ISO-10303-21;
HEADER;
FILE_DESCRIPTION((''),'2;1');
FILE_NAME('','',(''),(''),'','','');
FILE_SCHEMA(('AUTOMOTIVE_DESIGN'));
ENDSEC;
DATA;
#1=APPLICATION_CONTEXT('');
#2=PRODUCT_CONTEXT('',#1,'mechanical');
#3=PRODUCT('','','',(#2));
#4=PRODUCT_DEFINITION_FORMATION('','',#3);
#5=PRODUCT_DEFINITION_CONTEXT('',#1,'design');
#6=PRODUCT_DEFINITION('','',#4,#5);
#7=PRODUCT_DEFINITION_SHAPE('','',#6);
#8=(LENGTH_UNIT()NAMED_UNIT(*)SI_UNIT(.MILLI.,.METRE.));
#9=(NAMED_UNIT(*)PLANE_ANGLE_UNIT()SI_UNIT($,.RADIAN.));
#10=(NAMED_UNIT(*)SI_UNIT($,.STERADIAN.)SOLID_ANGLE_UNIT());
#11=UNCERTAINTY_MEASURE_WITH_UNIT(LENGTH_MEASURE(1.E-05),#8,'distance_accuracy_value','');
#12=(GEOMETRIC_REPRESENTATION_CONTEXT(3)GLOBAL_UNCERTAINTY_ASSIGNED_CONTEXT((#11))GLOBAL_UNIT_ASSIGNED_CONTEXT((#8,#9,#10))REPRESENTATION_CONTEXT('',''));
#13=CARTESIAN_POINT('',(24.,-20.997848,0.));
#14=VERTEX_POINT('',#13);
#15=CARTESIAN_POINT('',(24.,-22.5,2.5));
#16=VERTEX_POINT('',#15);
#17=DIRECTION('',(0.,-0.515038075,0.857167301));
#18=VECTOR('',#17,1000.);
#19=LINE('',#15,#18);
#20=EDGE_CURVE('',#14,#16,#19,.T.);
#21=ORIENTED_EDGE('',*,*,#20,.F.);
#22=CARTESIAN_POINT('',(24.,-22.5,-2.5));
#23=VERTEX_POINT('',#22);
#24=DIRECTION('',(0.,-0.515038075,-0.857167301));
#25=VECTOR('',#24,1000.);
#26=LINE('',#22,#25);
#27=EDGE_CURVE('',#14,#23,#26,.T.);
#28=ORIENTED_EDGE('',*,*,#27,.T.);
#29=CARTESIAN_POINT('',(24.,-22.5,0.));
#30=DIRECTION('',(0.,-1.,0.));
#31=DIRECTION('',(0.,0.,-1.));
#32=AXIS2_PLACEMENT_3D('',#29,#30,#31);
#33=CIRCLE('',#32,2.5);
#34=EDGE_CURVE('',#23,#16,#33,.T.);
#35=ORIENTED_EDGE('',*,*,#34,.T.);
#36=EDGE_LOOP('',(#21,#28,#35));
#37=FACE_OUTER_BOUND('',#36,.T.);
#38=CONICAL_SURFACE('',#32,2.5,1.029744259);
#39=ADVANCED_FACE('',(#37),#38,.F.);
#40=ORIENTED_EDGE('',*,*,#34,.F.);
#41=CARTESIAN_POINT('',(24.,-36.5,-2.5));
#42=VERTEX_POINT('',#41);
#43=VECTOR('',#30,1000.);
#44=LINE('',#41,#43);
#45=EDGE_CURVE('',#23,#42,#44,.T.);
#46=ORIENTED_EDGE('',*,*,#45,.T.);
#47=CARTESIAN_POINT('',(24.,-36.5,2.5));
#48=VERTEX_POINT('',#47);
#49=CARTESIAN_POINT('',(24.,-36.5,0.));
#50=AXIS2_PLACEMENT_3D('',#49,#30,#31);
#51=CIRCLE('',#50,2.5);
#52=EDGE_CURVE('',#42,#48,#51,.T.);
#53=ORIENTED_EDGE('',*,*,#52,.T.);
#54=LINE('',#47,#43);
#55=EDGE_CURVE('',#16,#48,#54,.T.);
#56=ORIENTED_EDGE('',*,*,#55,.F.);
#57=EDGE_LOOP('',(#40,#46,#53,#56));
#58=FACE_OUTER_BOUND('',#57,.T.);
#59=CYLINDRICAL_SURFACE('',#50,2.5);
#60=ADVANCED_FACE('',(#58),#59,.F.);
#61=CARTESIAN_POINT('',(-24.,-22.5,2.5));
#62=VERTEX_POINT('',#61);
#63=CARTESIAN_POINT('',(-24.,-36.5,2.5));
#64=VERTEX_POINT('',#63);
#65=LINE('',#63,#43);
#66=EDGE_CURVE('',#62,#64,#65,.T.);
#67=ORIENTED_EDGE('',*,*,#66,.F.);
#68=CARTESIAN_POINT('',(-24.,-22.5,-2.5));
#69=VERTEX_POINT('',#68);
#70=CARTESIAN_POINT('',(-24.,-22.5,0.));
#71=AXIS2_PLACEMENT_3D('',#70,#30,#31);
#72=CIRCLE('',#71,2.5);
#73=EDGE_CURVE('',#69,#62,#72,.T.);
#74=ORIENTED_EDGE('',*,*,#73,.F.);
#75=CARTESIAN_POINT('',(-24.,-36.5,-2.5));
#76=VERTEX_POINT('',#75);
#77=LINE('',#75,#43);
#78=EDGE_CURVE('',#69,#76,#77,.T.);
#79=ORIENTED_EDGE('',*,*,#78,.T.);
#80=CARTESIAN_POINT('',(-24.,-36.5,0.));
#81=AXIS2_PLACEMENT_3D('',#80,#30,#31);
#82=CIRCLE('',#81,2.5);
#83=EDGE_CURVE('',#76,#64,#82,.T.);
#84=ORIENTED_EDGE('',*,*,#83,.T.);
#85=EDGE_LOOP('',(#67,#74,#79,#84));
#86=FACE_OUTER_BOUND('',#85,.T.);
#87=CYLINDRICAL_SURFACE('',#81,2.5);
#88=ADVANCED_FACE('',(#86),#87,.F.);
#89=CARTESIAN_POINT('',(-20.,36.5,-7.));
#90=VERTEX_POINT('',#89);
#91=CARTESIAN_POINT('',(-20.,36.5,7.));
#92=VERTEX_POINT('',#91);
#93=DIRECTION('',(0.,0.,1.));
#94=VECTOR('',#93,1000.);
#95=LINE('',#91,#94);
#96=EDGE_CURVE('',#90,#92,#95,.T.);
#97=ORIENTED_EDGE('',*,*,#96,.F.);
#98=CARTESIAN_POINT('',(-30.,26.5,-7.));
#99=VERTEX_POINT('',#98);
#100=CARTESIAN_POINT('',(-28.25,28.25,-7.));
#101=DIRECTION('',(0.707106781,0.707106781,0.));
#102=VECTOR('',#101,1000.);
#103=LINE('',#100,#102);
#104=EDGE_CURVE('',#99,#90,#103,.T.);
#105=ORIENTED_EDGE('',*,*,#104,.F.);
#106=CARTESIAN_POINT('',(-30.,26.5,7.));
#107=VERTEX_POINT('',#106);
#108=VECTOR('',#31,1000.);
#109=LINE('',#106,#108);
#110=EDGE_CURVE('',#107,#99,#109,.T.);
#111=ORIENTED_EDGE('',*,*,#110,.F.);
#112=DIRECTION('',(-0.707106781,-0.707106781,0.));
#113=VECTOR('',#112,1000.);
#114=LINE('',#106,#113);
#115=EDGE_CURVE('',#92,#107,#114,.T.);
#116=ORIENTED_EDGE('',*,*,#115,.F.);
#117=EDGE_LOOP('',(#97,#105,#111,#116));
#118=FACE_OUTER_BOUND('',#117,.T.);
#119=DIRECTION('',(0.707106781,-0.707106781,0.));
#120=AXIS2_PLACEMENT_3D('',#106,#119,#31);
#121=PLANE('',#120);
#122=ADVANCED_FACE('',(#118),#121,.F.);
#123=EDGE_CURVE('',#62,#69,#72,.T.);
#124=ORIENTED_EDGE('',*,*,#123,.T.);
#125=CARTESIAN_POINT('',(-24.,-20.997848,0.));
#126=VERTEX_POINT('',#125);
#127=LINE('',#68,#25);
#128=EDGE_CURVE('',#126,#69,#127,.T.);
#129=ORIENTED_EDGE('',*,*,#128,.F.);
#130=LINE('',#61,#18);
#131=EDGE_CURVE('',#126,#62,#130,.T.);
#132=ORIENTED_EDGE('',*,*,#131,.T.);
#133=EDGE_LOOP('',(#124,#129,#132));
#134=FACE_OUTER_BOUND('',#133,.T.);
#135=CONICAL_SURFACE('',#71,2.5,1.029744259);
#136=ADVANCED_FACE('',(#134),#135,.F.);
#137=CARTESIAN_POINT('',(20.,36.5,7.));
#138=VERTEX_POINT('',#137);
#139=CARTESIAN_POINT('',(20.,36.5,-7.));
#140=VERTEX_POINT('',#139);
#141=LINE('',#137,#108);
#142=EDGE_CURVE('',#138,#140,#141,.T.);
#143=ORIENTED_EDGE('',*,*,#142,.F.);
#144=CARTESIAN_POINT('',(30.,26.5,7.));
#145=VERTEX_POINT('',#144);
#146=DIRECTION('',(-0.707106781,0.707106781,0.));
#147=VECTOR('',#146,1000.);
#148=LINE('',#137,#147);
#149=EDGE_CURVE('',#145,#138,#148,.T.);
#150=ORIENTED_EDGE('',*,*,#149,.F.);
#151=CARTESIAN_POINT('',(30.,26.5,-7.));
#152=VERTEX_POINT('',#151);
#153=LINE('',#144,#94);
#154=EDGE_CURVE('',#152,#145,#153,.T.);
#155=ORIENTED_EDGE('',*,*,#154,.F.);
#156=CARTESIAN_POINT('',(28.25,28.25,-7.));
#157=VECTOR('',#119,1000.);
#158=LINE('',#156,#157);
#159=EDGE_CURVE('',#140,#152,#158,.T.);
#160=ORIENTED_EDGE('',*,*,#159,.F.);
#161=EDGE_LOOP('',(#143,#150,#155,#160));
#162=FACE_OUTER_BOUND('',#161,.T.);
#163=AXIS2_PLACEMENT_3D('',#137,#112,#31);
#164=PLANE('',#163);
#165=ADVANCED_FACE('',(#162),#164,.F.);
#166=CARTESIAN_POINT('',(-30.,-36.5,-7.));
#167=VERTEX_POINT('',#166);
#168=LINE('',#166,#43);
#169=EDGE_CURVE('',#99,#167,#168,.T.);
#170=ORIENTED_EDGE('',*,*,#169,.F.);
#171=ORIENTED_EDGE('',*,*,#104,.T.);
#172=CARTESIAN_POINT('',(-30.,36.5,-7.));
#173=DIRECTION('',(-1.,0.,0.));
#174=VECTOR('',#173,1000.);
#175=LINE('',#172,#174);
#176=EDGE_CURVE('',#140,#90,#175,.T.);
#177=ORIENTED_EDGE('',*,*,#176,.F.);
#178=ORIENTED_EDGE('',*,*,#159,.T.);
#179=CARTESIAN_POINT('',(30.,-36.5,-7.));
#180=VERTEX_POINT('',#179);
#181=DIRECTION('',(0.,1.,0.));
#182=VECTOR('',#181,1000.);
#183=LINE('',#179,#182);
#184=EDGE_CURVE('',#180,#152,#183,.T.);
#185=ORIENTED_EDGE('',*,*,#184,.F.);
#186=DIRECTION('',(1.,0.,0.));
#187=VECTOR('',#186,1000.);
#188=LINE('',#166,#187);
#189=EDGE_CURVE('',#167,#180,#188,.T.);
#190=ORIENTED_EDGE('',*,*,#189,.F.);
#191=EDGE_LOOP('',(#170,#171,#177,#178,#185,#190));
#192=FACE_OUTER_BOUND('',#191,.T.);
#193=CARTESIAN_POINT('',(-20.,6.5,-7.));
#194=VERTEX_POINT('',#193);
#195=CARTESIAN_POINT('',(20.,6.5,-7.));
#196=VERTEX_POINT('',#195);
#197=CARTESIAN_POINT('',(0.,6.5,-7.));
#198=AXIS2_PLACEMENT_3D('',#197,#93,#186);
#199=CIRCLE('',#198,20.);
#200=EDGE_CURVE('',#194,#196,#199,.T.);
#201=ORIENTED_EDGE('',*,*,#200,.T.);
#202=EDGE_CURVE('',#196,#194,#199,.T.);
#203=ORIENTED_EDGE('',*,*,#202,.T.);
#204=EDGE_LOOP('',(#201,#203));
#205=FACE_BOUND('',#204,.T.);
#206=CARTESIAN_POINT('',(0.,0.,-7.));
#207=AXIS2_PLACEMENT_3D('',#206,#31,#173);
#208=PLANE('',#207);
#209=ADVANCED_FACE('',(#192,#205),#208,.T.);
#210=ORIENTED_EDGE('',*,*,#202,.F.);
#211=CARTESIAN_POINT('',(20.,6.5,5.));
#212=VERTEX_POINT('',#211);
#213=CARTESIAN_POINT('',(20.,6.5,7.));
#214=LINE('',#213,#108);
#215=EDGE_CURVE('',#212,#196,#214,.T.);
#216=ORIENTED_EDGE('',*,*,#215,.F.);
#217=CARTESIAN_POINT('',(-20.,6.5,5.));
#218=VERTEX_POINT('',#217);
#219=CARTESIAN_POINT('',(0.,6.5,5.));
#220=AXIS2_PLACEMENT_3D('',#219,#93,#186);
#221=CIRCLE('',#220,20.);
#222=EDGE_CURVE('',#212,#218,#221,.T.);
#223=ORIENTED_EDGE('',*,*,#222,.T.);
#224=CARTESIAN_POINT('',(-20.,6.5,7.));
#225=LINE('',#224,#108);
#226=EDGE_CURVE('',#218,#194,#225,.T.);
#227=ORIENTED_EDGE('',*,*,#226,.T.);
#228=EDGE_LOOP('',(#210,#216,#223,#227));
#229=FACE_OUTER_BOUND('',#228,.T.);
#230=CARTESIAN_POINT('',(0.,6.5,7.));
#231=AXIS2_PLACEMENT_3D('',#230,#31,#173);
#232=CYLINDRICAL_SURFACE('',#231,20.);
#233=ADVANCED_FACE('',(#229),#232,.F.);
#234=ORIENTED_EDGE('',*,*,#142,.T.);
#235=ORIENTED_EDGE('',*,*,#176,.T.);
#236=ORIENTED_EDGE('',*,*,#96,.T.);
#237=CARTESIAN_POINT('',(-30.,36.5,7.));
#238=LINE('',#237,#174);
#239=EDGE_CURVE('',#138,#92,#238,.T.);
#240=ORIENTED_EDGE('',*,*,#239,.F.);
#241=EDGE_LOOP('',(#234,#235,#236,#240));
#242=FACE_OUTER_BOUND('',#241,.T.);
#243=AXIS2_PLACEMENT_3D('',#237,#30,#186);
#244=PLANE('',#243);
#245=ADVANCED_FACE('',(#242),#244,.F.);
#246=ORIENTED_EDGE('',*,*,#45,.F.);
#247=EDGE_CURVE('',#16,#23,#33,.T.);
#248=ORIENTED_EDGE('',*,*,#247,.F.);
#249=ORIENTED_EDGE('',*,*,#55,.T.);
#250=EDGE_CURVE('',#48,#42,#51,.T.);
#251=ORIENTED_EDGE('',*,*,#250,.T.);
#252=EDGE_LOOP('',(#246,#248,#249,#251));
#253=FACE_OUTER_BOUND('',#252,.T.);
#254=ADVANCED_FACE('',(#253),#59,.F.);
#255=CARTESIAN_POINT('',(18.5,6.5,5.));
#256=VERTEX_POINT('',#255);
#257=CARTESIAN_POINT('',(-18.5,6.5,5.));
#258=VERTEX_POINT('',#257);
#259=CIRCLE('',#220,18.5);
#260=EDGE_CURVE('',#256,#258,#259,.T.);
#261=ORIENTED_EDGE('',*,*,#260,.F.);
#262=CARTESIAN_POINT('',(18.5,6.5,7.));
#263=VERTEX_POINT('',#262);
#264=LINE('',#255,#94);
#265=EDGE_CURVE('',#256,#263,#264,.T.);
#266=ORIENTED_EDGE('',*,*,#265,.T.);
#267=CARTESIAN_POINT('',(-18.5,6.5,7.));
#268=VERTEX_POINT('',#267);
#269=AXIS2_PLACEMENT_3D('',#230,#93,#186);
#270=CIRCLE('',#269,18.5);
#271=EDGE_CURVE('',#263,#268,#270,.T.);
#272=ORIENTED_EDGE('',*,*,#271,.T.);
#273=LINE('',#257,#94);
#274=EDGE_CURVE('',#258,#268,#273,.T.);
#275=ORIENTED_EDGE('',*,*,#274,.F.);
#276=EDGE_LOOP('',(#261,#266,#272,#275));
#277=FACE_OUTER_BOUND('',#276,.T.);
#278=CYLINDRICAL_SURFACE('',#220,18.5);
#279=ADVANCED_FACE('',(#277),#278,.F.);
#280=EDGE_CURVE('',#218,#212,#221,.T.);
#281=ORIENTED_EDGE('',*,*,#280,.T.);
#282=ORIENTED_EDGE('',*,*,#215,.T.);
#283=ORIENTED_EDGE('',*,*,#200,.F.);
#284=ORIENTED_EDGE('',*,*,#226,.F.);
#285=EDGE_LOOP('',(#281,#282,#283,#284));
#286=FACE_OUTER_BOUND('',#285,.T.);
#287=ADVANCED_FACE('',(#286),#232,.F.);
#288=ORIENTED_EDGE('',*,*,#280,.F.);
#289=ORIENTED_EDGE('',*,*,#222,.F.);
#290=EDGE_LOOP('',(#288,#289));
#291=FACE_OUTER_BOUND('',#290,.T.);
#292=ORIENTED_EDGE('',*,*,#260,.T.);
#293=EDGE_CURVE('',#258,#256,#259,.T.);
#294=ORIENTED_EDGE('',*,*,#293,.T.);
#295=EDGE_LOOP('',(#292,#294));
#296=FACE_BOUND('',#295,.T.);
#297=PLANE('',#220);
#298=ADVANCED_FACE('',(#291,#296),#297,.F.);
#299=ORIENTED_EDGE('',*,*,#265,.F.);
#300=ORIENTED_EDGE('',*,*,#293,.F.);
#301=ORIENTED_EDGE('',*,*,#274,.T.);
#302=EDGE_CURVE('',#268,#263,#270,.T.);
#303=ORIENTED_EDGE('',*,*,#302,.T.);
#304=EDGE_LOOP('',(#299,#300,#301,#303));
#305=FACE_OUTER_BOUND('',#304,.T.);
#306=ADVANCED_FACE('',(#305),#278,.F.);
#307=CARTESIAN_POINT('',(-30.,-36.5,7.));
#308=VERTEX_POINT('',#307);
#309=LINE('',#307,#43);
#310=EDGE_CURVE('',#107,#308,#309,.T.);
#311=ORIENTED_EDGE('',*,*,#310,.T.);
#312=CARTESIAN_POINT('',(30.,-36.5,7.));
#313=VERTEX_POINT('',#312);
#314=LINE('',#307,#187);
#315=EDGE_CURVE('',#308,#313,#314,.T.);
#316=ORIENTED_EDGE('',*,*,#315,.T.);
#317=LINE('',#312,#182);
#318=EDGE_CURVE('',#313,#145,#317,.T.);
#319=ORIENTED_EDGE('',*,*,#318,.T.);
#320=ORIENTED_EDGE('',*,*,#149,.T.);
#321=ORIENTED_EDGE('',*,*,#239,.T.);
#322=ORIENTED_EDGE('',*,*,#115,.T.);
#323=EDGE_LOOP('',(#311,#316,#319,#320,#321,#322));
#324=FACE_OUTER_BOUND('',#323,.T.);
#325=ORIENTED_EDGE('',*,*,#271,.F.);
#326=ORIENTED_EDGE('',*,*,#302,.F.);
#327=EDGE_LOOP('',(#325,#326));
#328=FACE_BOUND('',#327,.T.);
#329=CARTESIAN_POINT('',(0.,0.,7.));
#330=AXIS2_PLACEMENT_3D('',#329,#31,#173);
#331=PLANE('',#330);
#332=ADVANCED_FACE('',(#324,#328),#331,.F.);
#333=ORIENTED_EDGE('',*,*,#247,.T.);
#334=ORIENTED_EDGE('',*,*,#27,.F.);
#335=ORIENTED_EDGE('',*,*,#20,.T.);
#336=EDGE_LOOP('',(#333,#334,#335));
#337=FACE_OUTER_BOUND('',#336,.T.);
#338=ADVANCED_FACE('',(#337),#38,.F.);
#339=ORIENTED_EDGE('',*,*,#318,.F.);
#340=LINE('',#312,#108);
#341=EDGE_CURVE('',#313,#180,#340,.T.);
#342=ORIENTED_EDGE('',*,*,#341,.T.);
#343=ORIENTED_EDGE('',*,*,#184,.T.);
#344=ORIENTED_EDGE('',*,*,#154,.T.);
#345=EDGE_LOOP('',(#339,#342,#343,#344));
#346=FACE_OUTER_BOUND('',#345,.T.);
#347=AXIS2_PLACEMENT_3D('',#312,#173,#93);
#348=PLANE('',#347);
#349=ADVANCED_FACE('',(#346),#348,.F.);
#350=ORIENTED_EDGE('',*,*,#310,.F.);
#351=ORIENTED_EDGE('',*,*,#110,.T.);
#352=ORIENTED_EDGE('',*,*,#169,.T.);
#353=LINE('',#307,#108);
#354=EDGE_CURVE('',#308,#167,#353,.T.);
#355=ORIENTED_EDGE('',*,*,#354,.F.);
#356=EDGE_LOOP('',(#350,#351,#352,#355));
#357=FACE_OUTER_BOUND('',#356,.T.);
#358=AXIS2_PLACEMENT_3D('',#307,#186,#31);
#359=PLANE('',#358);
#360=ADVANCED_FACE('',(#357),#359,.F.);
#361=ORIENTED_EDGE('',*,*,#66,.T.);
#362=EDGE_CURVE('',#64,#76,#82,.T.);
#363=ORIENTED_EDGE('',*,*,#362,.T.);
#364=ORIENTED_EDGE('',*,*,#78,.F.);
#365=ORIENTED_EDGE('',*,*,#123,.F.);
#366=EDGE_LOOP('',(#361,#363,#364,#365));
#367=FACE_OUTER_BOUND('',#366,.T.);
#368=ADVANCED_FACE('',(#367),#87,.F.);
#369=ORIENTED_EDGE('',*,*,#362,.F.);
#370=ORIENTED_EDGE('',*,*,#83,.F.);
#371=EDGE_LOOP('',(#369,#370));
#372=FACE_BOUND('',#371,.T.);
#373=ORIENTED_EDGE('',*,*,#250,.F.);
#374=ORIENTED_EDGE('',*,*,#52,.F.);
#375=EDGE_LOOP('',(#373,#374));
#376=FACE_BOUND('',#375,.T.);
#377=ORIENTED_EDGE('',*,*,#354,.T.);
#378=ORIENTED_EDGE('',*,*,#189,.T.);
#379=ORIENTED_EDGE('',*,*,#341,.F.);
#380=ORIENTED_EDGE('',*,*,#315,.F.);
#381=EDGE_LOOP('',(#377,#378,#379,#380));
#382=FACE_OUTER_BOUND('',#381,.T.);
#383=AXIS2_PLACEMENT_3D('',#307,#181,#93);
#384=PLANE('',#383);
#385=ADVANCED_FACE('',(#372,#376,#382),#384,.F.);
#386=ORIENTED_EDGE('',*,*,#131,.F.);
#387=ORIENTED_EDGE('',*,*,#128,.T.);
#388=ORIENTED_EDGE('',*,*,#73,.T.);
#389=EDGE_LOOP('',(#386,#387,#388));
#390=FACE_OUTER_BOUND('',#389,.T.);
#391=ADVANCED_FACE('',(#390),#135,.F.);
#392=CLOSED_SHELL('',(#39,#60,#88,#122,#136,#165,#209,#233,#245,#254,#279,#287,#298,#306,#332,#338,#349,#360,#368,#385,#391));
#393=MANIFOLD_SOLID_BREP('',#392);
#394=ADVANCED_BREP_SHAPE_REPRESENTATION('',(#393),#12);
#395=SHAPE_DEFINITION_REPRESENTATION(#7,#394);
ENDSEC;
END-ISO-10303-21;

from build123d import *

# Parameters (mm, degrees)
SKETCH_1_W             = 60
SKETCH_1_H             = 73
SKETCH_1_R             = 20
EXTRUDE_1_DEPTH        = 7
EXTRUDE_START          = -2
SKETCH_2_R             = 20
SKETCH_2_R_2           = 18.5
EXTRUDE_2_DEPTH        = 2
CHAMFER_1_SIZE         = 10
HOLE_WIZARD_M6_1_D     = 5
HOLE_WIZARD_M6_1_DEPTH = 14
HOLE_WIZARD_M6_1_TIP   = 1.502151548


with BuildPart() as part:
    # 草图1 → 凸台-拉伸1 (new, symmetric)
    with BuildSketch(Plane.XY):
        Rectangle(SKETCH_1_W, SKETCH_1_H)
        with Locations((0, 6.5)):
            Circle(SKETCH_1_R, mode=Mode.SUBTRACT)
    extrude(amount=EXTRUDE_1_DEPTH, both=True)

    # 草图2 → 凸台-拉伸2 (add)
    with BuildSketch(Plane.XY.offset(7).offset(EXTRUDE_START)):
        with Locations((0, 6.5)):
            Circle(SKETCH_2_R)
        with Locations((0, 6.5)):
            Circle(SKETCH_2_R_2, mode=Mode.SUBTRACT)
    extrude(amount=EXTRUDE_2_DEPTH)

    # 倒角1
    chamfer_1_edges = [part.edges().sort_by_distance(p)[0] for p in [
        (-30, 36.5, 0),
        (30, 36.5, 0),
    ]]
    chamfer(chamfer_1_edges, length=CHAMFER_1_SIZE)

    # M6 螺纹孔1
    with Locations(Plane(origin=(-24, -36.5, 0), x_dir=(0, 0, -1), z_dir=(0, -1, 0))):
        with Locations((0, 0), (0, 48)):
            Hole(HOLE_WIZARD_M6_1_D / 2, depth=HOLE_WIZARD_M6_1_DEPTH)
            with Locations((0, 0, -(HOLE_WIZARD_M6_1_DEPTH + HOLE_WIZARD_M6_1_TIP / 2))):  # 118° drill point
                Cone(0, HOLE_WIZARD_M6_1_D / 2, HOLE_WIZARD_M6_1_TIP, mode=Mode.SUBTRACT)


solid = part.part
